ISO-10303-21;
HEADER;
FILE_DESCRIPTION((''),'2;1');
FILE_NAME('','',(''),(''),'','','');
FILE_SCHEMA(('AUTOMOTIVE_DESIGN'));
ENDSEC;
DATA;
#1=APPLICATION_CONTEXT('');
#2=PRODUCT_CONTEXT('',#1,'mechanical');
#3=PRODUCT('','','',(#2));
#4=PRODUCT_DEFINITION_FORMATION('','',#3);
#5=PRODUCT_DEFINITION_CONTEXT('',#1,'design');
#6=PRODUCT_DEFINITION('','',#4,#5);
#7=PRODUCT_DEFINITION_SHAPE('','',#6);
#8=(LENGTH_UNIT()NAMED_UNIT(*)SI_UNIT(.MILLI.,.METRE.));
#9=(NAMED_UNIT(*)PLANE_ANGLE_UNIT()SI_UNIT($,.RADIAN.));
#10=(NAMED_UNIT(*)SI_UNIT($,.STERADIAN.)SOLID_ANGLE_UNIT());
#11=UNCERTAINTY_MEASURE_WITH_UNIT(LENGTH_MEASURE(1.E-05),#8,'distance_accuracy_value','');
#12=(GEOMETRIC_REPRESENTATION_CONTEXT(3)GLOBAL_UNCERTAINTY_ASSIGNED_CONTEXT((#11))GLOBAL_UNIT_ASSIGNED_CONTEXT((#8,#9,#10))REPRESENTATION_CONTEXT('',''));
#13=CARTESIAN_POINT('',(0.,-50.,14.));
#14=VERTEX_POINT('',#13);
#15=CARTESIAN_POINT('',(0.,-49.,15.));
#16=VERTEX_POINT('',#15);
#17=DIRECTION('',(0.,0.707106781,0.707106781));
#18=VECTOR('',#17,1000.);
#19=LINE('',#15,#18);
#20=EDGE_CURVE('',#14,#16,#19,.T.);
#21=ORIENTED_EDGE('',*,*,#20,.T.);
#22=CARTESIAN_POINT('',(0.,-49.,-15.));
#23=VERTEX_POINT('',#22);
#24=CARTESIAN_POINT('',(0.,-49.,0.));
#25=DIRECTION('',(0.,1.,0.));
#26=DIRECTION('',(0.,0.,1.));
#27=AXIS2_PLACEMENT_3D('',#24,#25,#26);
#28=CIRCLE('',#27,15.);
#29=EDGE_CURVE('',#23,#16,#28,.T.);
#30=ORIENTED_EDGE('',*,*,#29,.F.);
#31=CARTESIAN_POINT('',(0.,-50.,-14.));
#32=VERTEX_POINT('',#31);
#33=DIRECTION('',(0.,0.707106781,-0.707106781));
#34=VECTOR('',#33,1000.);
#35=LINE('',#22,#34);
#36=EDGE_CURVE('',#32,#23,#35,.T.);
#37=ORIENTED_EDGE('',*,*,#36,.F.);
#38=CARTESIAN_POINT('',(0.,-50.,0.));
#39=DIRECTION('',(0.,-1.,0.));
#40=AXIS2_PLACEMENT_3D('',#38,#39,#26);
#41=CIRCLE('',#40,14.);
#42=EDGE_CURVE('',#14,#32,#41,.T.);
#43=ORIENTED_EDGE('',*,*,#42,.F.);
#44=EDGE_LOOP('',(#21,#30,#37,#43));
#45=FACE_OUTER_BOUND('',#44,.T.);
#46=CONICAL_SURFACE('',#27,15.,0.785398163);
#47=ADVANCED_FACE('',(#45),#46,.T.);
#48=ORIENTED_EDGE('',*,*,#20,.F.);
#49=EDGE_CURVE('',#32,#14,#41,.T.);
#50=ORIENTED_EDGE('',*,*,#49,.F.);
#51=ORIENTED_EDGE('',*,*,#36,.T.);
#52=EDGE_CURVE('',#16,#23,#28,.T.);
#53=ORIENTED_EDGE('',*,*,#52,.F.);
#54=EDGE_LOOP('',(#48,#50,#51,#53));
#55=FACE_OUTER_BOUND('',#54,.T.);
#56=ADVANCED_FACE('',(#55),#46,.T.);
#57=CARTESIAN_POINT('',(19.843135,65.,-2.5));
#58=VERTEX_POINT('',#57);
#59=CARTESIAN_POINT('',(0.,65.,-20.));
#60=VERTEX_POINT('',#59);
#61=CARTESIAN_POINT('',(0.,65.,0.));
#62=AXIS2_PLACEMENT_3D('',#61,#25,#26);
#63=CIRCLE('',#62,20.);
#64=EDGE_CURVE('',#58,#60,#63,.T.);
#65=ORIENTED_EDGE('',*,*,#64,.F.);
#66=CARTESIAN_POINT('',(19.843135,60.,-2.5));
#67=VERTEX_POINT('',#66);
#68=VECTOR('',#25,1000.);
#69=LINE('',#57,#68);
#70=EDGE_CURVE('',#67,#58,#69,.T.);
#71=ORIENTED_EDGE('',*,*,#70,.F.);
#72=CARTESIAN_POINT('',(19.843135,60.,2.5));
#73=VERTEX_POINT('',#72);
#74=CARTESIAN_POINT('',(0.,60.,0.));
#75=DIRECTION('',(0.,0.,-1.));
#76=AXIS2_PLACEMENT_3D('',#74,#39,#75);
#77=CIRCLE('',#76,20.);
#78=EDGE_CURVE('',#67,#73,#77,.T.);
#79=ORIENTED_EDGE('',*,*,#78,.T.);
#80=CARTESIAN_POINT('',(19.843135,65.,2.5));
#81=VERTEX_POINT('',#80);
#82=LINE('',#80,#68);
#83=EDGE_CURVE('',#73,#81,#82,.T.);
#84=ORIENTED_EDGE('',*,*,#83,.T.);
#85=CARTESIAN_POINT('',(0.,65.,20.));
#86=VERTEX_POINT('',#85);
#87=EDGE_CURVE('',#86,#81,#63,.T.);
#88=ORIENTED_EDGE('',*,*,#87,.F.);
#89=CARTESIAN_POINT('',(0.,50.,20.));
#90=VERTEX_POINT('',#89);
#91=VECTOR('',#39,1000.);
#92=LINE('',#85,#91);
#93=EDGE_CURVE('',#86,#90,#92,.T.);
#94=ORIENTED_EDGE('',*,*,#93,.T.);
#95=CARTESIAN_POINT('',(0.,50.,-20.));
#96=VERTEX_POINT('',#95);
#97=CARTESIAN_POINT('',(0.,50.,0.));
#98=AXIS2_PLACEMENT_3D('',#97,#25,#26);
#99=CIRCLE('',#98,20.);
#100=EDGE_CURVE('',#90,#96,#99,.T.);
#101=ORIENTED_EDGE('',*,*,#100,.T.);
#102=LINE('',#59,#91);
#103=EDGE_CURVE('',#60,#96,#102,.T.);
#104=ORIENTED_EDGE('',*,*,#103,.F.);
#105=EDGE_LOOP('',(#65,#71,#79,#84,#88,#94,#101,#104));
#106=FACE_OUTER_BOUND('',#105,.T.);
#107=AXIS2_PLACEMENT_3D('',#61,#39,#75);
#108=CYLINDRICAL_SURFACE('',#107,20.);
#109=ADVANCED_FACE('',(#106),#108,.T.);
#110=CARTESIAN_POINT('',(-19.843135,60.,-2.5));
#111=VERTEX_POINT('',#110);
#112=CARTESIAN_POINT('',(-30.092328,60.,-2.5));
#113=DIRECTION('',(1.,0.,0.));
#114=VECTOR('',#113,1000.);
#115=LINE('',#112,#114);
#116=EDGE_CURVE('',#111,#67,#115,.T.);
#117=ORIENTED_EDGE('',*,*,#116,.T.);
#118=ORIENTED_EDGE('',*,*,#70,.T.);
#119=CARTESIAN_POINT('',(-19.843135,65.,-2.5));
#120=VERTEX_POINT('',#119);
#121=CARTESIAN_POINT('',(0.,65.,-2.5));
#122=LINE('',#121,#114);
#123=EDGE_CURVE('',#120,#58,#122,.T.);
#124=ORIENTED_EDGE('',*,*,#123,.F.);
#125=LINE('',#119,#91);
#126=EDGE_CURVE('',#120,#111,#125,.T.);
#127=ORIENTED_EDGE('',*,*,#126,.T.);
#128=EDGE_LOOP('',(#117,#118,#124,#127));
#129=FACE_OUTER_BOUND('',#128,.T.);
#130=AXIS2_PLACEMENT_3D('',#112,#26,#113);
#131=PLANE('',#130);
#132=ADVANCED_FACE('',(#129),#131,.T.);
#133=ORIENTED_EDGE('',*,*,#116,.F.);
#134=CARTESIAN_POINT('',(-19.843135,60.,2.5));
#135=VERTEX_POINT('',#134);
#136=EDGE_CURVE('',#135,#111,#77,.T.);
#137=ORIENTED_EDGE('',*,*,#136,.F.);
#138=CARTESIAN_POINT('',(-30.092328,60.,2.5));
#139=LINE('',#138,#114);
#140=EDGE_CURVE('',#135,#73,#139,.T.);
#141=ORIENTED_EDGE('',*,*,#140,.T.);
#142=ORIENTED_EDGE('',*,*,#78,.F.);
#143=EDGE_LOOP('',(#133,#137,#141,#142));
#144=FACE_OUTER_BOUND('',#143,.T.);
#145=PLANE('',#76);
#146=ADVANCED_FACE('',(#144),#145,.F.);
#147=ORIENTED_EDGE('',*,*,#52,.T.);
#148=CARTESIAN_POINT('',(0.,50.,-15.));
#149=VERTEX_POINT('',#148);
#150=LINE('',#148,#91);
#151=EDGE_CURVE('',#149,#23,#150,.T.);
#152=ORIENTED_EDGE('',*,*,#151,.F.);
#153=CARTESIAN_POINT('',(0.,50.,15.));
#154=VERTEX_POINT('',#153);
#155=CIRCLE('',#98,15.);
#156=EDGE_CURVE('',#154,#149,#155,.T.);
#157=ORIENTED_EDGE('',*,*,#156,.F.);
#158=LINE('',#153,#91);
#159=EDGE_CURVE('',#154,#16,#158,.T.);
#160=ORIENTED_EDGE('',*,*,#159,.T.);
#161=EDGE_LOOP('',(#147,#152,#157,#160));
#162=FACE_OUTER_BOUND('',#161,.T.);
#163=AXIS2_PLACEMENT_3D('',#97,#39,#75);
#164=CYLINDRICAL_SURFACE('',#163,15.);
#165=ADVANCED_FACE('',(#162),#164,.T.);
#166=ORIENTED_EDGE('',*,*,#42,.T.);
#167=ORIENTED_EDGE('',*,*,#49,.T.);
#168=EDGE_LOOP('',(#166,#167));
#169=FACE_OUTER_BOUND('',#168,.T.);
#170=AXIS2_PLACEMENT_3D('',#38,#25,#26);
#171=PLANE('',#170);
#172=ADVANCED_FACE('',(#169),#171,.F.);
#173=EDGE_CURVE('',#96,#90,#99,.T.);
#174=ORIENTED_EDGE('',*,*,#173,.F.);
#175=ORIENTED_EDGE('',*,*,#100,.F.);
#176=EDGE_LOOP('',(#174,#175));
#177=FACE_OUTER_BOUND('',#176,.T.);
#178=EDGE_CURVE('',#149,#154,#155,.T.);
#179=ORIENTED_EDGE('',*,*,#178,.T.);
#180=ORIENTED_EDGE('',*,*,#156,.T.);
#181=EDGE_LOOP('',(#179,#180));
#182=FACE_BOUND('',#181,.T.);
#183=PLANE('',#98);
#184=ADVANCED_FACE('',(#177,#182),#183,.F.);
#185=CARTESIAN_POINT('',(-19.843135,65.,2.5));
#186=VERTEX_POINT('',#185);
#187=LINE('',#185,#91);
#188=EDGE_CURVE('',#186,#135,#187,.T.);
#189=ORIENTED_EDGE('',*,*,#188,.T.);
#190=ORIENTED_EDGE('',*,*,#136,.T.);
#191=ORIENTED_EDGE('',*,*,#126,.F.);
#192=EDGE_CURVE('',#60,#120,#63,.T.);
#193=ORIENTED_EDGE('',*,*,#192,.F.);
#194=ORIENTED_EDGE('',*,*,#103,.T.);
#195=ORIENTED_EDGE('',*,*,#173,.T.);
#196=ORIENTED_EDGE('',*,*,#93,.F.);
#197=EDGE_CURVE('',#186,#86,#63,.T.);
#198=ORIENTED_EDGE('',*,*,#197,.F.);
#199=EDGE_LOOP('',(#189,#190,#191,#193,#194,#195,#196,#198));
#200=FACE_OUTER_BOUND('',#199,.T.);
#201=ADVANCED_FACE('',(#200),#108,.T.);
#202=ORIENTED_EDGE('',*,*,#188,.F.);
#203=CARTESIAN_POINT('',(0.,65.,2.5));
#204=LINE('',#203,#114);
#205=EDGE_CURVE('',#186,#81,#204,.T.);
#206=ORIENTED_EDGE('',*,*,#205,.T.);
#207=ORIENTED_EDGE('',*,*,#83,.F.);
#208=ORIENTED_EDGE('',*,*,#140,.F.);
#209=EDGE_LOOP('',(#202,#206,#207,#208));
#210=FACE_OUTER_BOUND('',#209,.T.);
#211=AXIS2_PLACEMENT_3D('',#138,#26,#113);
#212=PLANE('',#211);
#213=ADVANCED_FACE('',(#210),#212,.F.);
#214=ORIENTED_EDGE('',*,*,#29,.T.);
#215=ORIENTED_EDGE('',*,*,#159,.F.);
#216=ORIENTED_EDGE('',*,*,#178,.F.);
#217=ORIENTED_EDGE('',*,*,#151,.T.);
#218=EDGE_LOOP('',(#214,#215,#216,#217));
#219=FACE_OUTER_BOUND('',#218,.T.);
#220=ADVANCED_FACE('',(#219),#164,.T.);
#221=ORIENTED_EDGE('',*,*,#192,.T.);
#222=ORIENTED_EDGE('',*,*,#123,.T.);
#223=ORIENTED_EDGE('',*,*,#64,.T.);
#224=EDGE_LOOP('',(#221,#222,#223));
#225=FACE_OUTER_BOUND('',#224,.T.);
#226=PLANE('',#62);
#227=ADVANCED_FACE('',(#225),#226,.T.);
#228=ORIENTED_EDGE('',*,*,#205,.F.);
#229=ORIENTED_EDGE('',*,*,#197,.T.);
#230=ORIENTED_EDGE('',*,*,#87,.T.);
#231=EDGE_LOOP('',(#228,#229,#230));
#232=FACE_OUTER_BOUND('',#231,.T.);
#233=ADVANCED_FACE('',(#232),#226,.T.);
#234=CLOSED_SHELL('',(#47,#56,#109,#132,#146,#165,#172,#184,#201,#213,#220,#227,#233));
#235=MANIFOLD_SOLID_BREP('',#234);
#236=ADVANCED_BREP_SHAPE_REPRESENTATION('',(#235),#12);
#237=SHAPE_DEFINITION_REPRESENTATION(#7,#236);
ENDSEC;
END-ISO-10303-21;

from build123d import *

# Parameters (mm, degrees)
SKETCH_1_R          = 15
EXTRUDE_1_DEPTH     = 50
SKETCH_2_R          = 20
EXTRUDE_2_DEPTH     = 15
SKETCH_3_W          = 60.184655206
SKETCH_3_H          = 5
CUT_EXTRUDE_1_DEPTH = 5
CHAMFER_1_SIZE      = 1


with BuildPart() as part:
    # 草图1 → 凸台-拉伸1 (new, symmetric)
    with BuildSketch(Plane(origin=(0, 0, 0), x_dir=(1, 0, 0), z_dir=(0, 1, 0))):
        with Locations(Location((0, 0, 0), (0, 0, 270))):
            Circle(SKETCH_1_R)
    extrude(amount=EXTRUDE_1_DEPTH, both=True)

    # 草图2 → 凸台-拉伸2 (add)
    with BuildSketch(Plane(origin=(0, 50, 0), x_dir=(1, 0, 0), z_dir=(0, 1, 0))):
        with Locations(Location((0, 0, 0), (0, 0, 270))):
            Circle(SKETCH_2_R)
    extrude(amount=EXTRUDE_2_DEPTH)

    # 草图3 → 切除-拉伸1 (cut)
    with BuildSketch(Plane(origin=(0, 65, 0), x_dir=(1, 0, 0), z_dir=(0, 1, 0))):
        Rectangle(SKETCH_3_W, SKETCH_3_H)
    extrude(amount=-CUT_EXTRUDE_1_DEPTH, mode=Mode.SUBTRACT)

    # 倒角1
    chamfer_1_edges = [part.edges().sort_by_distance(p)[0] for p in [
        (0, -50, -15),
    ]]
    chamfer(chamfer_1_edges, length=CHAMFER_1_SIZE)


solid = part.part
